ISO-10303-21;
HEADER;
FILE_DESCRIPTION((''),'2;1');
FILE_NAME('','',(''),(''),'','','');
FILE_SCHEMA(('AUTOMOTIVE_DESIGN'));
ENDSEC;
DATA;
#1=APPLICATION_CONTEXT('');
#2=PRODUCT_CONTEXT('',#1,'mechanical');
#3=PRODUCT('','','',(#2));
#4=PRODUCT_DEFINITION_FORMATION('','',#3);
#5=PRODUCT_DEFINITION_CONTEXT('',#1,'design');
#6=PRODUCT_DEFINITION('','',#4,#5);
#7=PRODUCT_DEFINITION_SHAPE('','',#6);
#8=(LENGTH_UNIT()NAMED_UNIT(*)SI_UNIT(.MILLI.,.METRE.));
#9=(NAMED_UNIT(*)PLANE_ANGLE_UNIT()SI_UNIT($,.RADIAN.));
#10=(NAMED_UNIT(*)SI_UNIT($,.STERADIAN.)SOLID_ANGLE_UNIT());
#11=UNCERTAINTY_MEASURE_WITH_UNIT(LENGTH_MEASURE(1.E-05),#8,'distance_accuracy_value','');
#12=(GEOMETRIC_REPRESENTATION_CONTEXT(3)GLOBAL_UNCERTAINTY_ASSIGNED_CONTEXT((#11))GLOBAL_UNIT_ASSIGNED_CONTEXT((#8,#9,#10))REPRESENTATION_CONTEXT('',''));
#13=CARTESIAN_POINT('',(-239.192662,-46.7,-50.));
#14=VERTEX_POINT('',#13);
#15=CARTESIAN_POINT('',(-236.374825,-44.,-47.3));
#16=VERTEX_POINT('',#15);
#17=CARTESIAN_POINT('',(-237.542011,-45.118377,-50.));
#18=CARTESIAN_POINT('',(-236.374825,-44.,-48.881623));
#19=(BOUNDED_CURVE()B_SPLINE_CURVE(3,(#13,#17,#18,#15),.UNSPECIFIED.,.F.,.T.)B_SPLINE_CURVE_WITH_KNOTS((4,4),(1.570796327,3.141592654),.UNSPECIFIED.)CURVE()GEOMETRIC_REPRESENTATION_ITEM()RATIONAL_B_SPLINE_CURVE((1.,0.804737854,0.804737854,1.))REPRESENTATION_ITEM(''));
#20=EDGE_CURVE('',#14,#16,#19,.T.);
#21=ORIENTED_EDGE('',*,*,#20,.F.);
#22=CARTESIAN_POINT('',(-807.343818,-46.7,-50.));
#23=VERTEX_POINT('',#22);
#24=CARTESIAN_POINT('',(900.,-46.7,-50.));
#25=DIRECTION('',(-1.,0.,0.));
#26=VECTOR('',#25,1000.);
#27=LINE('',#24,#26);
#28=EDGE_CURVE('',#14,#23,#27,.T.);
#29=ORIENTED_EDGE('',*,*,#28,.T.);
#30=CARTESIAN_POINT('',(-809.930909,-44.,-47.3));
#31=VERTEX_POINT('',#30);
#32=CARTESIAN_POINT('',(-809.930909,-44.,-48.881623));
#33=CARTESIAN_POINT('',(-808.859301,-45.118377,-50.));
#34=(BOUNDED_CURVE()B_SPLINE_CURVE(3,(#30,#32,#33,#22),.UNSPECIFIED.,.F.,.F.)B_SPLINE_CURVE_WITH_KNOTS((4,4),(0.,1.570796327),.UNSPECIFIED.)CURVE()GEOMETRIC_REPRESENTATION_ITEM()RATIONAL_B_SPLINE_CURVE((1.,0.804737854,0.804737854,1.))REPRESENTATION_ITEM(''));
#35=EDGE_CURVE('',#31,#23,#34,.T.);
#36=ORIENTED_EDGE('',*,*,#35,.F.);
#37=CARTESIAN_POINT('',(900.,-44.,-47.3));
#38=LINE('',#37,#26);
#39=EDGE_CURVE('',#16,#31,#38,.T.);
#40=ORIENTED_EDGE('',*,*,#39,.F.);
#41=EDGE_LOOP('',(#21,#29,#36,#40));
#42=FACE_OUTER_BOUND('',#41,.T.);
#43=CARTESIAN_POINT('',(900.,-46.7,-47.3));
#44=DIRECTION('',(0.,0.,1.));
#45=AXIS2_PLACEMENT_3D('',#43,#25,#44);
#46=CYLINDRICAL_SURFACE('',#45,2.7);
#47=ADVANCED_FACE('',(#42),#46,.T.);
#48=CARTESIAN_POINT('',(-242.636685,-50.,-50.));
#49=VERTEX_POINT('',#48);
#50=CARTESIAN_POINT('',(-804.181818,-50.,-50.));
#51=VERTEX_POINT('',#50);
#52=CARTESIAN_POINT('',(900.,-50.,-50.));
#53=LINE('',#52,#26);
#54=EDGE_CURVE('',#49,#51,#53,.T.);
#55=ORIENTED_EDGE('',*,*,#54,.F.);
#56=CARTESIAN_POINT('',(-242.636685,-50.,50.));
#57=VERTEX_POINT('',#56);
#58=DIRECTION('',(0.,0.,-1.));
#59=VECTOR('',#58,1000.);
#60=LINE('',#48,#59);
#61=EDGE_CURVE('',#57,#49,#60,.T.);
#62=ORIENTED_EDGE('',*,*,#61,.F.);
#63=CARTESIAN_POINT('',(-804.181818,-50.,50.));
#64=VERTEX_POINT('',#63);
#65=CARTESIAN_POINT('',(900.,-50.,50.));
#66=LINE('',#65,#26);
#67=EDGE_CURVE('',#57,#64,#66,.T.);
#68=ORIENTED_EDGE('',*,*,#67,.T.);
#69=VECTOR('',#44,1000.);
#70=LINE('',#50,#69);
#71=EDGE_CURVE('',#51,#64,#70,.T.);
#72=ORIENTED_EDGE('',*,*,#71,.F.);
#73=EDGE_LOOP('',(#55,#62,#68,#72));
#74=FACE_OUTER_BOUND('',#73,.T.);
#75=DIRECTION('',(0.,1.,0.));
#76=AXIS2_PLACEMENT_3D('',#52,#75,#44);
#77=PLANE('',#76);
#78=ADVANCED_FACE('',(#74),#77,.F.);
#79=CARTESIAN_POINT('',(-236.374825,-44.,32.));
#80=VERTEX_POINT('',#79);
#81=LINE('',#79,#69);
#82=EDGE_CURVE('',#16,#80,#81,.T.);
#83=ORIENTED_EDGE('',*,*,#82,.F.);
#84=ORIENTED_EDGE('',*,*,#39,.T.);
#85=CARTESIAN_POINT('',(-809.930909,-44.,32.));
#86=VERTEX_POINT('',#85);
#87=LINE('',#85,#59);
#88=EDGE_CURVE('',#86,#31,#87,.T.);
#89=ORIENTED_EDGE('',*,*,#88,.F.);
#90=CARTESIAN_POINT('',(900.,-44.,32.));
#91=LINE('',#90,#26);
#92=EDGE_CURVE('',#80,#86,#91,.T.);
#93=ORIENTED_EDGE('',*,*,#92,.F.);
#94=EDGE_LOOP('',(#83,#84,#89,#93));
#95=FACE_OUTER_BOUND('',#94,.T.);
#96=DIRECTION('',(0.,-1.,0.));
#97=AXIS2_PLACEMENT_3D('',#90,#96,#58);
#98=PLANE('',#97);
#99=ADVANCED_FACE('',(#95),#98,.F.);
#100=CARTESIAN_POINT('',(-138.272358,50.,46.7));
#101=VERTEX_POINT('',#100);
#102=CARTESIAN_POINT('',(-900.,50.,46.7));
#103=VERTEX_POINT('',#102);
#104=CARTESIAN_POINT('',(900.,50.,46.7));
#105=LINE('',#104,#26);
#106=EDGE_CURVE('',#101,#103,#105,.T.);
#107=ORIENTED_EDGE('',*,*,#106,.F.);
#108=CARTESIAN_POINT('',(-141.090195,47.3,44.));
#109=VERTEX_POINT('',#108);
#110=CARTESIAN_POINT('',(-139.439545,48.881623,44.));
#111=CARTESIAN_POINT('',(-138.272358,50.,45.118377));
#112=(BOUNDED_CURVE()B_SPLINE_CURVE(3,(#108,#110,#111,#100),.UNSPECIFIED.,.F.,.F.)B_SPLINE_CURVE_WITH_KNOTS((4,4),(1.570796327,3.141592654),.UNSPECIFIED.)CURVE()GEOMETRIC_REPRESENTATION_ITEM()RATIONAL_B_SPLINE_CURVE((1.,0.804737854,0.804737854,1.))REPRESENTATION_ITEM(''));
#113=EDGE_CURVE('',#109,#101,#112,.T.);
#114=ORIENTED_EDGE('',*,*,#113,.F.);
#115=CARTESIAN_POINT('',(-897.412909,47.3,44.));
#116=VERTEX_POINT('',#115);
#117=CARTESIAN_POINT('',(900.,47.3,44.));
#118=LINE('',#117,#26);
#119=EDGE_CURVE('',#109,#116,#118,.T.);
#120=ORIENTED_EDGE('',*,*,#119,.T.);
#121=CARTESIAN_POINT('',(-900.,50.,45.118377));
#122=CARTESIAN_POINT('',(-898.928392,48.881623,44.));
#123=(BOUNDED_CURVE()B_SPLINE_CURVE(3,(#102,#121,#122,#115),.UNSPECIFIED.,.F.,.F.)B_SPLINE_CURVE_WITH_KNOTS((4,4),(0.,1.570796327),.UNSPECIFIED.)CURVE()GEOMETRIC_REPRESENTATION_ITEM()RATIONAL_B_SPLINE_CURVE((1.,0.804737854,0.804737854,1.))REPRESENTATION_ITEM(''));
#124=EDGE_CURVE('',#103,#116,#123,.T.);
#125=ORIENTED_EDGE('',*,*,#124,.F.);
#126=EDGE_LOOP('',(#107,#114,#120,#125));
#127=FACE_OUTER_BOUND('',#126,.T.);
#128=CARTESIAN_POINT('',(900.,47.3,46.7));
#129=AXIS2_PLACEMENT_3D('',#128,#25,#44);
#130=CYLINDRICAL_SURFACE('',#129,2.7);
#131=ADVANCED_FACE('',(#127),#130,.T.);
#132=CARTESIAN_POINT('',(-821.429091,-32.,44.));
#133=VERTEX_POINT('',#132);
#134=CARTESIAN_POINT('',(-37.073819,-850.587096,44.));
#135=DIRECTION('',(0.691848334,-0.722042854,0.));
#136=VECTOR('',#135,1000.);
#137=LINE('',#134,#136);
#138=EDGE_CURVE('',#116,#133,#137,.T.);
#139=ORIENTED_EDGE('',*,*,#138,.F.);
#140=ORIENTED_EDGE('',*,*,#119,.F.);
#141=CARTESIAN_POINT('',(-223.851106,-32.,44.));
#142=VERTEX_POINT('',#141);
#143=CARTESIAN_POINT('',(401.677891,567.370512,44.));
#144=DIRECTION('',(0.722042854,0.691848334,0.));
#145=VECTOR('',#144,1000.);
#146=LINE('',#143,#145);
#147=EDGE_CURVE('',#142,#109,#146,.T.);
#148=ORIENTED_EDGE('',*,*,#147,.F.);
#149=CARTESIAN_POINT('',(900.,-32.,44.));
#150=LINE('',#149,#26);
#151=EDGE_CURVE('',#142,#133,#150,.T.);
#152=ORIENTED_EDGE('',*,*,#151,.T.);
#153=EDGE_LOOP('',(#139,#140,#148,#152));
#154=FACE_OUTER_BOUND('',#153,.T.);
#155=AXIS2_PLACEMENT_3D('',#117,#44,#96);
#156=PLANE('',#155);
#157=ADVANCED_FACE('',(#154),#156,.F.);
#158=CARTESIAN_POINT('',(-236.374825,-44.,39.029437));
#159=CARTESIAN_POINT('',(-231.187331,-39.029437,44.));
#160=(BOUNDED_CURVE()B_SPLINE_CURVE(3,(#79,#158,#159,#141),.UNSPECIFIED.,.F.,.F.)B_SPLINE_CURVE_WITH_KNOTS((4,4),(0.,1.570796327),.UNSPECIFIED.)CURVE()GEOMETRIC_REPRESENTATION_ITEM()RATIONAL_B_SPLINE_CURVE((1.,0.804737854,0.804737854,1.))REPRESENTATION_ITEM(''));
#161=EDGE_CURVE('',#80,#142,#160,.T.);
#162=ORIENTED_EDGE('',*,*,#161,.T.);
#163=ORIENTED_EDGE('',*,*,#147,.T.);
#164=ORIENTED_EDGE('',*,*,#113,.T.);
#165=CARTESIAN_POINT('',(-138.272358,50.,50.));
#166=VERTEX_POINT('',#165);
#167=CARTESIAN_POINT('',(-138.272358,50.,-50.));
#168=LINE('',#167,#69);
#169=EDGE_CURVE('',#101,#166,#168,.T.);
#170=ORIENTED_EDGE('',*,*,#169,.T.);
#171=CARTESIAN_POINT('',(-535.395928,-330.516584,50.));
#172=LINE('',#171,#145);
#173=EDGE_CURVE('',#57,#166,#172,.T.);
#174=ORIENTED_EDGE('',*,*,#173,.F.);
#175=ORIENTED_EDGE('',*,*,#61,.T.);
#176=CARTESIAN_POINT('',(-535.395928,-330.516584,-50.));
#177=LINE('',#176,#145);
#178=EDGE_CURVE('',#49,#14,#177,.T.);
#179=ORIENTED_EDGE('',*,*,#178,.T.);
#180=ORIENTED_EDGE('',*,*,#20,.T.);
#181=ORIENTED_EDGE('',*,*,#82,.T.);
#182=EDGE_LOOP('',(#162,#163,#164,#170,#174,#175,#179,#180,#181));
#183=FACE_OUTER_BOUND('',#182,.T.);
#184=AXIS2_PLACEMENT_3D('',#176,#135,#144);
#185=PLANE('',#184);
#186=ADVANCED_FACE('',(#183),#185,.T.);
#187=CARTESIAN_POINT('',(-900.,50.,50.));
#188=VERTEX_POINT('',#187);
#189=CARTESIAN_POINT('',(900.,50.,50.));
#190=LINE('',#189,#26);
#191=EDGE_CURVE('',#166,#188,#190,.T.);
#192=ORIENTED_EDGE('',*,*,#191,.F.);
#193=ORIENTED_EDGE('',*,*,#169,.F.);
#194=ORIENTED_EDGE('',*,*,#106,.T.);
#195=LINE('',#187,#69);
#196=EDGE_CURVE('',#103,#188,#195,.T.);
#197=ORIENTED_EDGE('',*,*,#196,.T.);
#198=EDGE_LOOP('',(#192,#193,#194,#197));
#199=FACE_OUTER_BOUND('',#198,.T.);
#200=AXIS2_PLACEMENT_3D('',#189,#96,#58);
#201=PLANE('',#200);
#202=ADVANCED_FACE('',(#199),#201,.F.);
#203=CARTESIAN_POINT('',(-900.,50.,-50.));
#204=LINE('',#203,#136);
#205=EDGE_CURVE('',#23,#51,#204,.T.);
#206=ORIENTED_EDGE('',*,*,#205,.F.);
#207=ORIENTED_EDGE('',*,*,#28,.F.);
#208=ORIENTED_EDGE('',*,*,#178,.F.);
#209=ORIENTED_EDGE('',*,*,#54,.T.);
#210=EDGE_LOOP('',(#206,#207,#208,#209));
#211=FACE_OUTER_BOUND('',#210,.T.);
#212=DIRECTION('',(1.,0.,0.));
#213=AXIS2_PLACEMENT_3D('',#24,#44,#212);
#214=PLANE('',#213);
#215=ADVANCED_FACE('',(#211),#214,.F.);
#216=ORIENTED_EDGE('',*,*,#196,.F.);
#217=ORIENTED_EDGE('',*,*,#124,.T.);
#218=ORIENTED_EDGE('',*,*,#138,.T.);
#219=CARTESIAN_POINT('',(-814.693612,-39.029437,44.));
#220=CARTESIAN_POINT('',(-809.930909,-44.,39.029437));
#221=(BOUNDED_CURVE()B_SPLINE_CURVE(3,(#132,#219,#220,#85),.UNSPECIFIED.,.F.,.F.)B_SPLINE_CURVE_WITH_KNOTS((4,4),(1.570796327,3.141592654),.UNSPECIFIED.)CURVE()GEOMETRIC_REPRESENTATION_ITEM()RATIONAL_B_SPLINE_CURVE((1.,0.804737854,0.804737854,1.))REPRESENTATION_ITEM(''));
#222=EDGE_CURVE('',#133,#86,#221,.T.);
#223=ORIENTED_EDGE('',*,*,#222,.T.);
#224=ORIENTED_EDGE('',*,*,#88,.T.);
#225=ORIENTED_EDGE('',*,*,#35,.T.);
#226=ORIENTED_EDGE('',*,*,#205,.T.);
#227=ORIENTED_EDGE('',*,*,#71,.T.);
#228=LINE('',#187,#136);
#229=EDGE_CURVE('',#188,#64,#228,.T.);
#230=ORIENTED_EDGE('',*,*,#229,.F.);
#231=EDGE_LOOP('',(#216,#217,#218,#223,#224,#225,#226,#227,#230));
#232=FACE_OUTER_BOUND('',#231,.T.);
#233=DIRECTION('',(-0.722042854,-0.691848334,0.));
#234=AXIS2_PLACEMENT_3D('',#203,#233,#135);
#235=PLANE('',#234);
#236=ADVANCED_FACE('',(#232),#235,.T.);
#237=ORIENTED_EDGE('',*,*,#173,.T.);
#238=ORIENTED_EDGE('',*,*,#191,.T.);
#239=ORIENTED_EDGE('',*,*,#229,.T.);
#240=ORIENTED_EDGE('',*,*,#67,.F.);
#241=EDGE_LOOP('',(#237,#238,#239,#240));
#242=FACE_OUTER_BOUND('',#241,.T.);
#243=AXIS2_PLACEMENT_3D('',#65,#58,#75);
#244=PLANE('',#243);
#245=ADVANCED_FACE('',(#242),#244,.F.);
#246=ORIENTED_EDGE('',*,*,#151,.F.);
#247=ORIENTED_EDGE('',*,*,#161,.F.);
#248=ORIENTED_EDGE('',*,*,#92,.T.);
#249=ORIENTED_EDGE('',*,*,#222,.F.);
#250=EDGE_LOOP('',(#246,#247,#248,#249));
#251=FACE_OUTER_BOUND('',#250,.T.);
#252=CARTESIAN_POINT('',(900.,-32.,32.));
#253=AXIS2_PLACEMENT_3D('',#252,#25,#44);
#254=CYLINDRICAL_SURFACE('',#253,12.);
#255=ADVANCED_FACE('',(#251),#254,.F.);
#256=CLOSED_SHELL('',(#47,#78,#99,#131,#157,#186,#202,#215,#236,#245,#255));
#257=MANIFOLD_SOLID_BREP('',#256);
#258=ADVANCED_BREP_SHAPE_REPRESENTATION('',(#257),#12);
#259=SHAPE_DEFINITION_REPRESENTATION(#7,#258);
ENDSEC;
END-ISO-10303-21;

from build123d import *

# Parameters (mm, degrees)
EXTRUDE1_DEPTH    = 900
SKETCH2_OUTSIDE_W = 2163.11
SKETCH2_OUTSIDE_H = 463.11
EXTRUDE5_DEPTH    = 100


with BuildPart() as part:
    # Sketch1 → Extrude1 (new, symmetric)
    with BuildSketch(Plane(origin=(0, 0, 0), x_dir=(0, 0, -1), z_dir=(1, 0, 0))):
        with BuildLine():
            Line((-44, 47.3), (-44, -32))
            ThreePointArc((-44, -32), (-40.485281374, -40.485281374), (-32, -44))
            Line((-32, -44), (47.3, -44))
            ThreePointArc((47.3, -44), (49.209188309, -44.790811691), (50, -46.7))
            Line((50, -46.7), (50, -50))
            Line((50, -50), (-50, -50))
            Line((-50, -50), (-50, 50))
            Line((-50, 50), (-46.7, 50))
            ThreePointArc((-46.7, 50), (-44.790811691, 49.209188309), (-44, 47.3))
        make_face()
    extrude(amount=EXTRUDE1_DEPTH, both=True)

    # Sketch2 outside → Extrude5 (cut)
    with BuildSketch(Plane.XY.offset(50)):
        Rectangle(SKETCH2_OUTSIDE_W, SKETCH2_OUTSIDE_H)
        Polygon((-138.272358385, 50), (-900, 50), (-535.395927853, -330.516583835), align=None, mode=Mode.SUBTRACT)
    extrude(amount=-EXTRUDE5_DEPTH, mode=Mode.SUBTRACT)


solid = part.part
